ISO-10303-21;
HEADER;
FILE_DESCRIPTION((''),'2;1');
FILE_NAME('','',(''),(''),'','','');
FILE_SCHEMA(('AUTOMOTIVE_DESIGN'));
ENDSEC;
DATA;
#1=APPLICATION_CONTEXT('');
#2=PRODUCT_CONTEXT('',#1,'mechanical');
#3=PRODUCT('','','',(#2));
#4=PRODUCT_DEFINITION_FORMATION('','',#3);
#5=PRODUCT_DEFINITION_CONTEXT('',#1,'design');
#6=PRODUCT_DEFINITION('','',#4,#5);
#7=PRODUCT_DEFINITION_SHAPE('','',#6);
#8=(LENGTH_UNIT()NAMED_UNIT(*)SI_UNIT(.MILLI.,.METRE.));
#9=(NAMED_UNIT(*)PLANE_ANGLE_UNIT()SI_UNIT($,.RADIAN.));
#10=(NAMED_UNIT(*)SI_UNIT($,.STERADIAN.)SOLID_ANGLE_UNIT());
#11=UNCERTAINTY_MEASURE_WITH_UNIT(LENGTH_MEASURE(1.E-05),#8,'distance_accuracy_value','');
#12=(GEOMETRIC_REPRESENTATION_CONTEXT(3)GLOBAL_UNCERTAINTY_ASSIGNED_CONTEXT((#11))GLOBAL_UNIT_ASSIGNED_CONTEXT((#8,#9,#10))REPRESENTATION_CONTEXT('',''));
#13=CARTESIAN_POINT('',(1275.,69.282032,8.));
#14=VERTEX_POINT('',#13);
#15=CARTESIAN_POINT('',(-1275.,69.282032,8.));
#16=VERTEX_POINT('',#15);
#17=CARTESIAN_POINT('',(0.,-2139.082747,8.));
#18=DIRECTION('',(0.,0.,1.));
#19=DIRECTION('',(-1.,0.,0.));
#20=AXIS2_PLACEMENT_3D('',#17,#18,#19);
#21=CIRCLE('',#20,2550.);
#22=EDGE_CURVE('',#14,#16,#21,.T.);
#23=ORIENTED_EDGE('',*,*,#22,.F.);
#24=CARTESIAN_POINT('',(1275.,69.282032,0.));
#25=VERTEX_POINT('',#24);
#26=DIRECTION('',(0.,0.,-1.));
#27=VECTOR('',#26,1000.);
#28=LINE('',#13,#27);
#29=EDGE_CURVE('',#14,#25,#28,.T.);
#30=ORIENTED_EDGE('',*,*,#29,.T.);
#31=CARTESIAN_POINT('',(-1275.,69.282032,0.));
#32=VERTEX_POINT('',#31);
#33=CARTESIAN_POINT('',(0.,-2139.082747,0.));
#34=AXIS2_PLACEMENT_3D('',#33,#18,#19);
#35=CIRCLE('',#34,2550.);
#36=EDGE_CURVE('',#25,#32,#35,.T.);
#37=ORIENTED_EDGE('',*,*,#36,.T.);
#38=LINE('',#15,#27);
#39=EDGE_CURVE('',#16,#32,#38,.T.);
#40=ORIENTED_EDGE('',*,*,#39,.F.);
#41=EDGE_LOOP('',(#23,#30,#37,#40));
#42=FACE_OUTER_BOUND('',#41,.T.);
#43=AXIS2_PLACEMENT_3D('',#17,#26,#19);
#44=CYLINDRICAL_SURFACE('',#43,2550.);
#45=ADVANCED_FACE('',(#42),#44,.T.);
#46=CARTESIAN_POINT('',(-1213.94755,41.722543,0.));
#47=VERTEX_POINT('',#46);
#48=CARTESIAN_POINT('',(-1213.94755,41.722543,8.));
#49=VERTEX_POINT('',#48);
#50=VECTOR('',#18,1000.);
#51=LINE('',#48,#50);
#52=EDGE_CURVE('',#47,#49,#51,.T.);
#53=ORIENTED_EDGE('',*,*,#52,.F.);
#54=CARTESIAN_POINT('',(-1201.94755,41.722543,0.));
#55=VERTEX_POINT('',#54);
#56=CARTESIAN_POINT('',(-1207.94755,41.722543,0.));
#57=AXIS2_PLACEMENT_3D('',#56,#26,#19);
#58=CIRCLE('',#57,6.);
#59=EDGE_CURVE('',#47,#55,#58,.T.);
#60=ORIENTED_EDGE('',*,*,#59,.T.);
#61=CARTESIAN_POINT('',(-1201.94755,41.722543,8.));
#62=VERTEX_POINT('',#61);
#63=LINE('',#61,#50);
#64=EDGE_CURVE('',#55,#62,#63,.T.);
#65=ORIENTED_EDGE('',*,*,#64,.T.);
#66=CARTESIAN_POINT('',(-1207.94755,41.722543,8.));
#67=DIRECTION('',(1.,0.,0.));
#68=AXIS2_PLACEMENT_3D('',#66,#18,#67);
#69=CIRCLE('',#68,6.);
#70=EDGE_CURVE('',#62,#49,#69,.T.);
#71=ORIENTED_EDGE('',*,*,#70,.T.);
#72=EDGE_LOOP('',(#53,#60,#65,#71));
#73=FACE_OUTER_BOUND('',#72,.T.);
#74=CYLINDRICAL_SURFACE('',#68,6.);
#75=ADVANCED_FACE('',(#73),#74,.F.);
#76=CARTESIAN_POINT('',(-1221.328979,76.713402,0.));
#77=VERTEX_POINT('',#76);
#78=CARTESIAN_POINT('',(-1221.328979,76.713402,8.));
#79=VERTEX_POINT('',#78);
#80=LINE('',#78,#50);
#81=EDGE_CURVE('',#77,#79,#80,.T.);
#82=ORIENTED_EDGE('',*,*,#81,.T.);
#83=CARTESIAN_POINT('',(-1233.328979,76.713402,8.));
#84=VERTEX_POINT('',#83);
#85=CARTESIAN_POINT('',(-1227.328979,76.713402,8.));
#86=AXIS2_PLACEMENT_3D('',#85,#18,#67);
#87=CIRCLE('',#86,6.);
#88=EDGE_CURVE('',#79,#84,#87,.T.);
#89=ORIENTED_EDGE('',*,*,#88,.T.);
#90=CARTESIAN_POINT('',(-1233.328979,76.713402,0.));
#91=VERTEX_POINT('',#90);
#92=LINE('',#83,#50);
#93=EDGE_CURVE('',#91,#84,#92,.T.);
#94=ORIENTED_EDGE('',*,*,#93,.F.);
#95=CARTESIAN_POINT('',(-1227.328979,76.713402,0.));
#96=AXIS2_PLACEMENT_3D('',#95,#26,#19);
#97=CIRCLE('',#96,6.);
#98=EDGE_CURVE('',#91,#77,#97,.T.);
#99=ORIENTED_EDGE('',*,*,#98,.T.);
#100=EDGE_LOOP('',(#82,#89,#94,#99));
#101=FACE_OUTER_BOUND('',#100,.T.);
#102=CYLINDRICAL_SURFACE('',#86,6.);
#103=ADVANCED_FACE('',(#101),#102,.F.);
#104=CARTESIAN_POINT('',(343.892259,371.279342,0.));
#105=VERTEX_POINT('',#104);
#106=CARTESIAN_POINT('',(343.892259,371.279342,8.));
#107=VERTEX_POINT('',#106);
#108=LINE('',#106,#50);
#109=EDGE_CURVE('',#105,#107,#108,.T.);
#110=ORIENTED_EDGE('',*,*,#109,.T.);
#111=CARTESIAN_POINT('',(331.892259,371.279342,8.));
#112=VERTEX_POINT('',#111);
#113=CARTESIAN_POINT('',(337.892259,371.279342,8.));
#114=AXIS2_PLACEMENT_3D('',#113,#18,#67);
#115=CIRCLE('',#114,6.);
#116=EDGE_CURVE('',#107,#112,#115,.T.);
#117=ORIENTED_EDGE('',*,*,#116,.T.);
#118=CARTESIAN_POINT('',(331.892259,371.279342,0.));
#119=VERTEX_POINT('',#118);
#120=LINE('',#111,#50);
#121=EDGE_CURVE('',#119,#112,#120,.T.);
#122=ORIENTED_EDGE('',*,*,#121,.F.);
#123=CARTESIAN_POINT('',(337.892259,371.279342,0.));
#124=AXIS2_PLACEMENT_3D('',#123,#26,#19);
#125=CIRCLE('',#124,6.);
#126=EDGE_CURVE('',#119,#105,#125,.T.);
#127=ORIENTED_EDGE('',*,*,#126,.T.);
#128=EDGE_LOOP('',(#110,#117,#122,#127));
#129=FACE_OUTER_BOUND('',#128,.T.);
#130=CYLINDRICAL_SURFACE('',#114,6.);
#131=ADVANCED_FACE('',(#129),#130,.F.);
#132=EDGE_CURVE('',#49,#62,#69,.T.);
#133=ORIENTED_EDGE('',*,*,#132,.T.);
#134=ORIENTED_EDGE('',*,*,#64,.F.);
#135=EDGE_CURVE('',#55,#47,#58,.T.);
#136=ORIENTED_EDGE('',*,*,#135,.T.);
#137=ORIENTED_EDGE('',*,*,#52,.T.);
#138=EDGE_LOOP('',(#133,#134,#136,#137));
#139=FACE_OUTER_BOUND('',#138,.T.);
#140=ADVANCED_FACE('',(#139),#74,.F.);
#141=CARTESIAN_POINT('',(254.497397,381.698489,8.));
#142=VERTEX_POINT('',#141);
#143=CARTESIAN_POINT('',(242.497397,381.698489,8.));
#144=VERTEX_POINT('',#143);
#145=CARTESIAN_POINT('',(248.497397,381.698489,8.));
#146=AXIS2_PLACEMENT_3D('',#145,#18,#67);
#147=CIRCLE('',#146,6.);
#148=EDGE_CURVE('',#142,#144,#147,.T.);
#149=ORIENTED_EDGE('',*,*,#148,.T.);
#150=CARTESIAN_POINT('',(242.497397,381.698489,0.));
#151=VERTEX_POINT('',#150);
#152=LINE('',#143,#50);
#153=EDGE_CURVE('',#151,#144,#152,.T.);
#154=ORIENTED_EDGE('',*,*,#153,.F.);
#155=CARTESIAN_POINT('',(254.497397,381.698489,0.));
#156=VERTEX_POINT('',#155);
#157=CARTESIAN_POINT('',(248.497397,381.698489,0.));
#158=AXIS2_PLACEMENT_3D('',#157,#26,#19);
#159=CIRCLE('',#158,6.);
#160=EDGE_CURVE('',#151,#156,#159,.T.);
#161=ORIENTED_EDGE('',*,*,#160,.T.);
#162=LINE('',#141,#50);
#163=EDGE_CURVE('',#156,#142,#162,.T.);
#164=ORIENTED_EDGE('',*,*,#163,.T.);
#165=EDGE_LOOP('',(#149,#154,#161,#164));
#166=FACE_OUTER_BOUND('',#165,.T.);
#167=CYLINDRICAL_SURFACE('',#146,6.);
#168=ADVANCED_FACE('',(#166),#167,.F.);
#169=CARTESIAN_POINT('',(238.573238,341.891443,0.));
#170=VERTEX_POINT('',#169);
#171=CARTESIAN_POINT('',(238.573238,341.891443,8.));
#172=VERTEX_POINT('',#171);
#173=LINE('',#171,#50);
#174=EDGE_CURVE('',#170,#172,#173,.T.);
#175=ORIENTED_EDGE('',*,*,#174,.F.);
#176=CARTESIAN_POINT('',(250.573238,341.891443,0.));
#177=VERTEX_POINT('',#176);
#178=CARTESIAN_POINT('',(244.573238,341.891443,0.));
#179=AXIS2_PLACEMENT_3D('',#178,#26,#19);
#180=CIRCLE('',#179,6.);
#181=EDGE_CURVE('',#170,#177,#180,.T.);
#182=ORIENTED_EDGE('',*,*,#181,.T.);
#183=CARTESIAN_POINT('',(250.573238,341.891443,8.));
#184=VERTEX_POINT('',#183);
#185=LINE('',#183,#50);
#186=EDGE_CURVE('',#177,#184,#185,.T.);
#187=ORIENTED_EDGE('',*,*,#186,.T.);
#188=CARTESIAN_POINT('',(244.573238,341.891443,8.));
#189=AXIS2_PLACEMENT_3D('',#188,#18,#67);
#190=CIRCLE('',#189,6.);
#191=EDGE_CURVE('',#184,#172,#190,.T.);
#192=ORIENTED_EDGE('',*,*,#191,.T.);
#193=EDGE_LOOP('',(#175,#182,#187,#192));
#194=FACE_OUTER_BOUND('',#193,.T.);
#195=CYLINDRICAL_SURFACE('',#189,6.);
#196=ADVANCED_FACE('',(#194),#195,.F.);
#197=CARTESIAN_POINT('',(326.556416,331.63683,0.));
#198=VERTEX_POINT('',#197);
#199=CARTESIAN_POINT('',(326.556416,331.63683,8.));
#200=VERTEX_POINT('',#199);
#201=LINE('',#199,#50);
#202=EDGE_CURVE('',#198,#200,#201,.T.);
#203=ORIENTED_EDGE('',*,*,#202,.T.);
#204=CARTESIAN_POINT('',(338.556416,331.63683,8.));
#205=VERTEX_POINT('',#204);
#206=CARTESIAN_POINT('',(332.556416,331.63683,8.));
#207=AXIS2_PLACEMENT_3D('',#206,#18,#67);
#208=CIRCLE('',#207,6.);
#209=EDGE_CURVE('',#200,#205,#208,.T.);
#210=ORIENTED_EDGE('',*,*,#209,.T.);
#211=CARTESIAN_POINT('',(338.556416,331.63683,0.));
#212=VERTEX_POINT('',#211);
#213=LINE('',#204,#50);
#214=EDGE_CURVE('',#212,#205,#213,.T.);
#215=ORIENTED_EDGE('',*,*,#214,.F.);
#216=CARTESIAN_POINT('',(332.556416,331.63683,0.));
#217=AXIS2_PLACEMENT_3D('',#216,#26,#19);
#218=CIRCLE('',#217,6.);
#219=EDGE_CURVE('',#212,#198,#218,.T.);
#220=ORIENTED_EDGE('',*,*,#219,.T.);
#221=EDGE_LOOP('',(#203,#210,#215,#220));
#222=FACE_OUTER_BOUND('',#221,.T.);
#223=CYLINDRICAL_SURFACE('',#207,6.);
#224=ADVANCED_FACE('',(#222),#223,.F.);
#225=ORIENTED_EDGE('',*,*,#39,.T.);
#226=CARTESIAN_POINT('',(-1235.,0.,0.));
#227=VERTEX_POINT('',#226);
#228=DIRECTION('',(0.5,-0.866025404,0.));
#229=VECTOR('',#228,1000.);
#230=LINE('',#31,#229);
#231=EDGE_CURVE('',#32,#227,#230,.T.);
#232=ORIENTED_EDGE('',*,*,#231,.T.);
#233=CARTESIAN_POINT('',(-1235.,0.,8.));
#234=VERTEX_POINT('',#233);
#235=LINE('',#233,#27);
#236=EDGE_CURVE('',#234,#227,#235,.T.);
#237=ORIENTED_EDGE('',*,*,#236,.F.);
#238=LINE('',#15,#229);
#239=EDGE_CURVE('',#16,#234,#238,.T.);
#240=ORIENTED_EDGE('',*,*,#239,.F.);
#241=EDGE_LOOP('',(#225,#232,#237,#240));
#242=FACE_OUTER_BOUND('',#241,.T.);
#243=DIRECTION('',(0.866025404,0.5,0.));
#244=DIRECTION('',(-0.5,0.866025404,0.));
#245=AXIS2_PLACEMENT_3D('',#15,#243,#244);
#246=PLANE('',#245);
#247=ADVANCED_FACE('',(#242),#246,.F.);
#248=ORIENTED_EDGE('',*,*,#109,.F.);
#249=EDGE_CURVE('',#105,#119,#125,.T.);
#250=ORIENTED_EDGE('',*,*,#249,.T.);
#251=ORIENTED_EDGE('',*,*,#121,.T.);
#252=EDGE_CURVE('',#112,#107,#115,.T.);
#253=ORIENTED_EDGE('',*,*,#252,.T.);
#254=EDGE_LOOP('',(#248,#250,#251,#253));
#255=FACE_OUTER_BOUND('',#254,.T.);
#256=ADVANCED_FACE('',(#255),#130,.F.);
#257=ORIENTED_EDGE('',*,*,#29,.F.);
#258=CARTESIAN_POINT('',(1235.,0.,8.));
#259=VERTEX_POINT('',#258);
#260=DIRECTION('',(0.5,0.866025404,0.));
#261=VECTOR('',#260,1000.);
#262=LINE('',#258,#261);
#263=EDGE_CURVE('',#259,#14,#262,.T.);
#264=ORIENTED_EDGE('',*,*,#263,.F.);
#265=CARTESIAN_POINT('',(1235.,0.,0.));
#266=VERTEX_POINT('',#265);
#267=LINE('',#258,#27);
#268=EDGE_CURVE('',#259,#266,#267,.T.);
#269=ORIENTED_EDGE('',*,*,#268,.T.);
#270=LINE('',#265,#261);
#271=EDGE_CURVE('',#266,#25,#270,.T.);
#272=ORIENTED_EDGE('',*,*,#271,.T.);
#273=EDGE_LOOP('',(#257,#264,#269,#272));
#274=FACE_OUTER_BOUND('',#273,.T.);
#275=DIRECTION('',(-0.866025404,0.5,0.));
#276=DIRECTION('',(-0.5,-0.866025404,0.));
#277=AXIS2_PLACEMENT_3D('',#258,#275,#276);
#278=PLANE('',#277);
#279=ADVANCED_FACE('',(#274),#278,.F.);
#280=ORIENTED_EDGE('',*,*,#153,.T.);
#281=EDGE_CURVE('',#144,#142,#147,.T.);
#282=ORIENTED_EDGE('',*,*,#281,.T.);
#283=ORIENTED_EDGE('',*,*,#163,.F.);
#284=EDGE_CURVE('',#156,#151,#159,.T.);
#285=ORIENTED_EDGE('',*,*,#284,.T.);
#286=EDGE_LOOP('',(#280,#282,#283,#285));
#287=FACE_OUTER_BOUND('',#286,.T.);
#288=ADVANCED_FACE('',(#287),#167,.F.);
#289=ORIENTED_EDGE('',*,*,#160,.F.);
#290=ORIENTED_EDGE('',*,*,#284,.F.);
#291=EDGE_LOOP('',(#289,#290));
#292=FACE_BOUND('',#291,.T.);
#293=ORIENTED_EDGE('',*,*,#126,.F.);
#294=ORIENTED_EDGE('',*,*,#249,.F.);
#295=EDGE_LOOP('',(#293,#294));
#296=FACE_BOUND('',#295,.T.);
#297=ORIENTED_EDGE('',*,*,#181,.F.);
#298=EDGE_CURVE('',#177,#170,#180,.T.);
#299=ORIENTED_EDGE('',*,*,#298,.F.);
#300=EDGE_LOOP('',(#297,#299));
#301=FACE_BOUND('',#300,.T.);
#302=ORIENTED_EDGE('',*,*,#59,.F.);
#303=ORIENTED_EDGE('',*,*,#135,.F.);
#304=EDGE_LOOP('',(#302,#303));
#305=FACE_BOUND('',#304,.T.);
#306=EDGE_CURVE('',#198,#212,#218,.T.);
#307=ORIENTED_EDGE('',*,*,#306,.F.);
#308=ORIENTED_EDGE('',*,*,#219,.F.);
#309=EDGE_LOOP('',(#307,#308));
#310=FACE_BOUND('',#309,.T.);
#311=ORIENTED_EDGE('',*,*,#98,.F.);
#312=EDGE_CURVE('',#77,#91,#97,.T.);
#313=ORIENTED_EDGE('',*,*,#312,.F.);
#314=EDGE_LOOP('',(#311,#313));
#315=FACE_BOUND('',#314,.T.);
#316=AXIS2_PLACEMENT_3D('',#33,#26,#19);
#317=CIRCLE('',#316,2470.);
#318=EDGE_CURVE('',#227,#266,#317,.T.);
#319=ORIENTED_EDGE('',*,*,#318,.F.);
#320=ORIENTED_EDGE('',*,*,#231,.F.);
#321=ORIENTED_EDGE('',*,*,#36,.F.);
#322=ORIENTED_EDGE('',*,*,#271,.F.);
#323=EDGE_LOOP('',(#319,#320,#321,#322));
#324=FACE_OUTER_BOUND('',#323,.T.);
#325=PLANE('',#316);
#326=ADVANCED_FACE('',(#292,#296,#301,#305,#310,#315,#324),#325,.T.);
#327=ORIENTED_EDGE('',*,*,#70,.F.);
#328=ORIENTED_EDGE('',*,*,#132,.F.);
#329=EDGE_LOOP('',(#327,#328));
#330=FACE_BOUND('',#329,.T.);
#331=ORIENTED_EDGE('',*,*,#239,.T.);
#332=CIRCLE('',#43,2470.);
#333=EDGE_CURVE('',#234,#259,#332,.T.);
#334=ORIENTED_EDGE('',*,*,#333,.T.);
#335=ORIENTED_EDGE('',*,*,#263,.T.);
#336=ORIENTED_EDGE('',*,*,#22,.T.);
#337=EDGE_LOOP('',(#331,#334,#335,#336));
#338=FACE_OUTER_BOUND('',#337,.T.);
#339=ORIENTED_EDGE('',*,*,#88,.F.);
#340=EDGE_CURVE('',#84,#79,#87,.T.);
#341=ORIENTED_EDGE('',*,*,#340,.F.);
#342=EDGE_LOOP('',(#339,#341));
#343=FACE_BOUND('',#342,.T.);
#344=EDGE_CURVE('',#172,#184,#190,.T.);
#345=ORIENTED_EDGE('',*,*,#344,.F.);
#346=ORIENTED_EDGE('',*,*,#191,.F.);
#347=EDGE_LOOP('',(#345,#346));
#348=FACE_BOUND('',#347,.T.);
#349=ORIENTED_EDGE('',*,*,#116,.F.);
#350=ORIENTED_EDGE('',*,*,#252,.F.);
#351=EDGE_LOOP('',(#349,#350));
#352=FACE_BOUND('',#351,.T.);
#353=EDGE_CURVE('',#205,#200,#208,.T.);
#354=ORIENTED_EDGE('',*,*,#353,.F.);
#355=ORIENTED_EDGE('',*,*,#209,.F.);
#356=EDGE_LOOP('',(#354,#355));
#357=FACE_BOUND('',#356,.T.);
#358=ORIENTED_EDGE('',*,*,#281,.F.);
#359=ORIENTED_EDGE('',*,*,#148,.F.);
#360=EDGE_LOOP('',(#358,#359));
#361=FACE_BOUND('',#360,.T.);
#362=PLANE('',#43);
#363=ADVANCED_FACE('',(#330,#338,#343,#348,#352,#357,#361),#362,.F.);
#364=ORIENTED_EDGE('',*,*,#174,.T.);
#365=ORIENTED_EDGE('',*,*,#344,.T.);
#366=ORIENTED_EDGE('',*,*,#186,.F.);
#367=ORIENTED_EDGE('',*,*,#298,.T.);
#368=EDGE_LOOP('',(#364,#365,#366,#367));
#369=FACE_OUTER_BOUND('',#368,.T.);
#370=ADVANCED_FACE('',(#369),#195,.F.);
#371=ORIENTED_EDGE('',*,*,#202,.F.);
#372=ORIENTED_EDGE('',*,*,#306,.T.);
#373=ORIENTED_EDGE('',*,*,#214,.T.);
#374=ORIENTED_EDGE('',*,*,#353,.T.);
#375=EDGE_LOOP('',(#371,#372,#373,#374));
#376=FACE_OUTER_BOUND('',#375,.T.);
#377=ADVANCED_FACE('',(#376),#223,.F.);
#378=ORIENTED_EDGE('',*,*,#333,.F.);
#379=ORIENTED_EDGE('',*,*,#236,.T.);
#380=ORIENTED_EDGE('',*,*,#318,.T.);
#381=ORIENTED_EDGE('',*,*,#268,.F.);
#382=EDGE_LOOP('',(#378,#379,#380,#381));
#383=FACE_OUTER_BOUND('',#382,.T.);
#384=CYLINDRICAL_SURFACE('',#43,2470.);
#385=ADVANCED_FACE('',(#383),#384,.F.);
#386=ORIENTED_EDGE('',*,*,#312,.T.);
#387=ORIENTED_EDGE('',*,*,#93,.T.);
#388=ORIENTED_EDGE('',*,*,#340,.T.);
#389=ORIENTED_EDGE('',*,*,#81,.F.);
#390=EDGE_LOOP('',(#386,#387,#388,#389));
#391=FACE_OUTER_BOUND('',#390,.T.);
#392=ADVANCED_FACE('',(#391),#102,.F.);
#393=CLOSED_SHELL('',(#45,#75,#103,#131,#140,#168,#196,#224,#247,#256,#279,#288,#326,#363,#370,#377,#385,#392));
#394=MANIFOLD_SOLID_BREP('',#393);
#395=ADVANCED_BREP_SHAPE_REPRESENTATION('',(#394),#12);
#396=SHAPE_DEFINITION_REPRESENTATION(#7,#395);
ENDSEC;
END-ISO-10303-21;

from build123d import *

# Parameters (mm, degrees)
BOSS_EXTRUDE1_DEPTH        = 8
F_12_0_12_DIAMETER_HOLE1_D = 12


with BuildPart() as part:
    # Sketch1 → Boss-Extrude1 (new body)
    with BuildSketch(Plane.XY):
        with BuildLine():
            Line((-1275, 69.282032303), (-1235, 0))
            ThreePointArc((-1235, 0), (0, 330.917252652), (1235, 0))
            Line((1235, 0), (1275, 69.282032303))
            ThreePointArc((1275, 69.282032303), (0, 410.917252652), (-1275, 69.282032303))
        make_face()
    extrude(amount=BOSS_EXTRUDE1_DEPTH)

    # Ø12.0 (12) Diameter Hole1 (through all)
    with Locations(Plane.XY.offset(8)):
        with Locations((-1227.328979234, 76.713402287), (-1207.947550426, 41.722543232), (248.497397062, 381.698489423), (244.573237614, 341.891442652), (337.892259182, 371.279342309), (332.556416163, 331.636830036)):
            Hole(F_12_0_12_DIAMETER_HOLE1_D / 2)


solid = part.part
